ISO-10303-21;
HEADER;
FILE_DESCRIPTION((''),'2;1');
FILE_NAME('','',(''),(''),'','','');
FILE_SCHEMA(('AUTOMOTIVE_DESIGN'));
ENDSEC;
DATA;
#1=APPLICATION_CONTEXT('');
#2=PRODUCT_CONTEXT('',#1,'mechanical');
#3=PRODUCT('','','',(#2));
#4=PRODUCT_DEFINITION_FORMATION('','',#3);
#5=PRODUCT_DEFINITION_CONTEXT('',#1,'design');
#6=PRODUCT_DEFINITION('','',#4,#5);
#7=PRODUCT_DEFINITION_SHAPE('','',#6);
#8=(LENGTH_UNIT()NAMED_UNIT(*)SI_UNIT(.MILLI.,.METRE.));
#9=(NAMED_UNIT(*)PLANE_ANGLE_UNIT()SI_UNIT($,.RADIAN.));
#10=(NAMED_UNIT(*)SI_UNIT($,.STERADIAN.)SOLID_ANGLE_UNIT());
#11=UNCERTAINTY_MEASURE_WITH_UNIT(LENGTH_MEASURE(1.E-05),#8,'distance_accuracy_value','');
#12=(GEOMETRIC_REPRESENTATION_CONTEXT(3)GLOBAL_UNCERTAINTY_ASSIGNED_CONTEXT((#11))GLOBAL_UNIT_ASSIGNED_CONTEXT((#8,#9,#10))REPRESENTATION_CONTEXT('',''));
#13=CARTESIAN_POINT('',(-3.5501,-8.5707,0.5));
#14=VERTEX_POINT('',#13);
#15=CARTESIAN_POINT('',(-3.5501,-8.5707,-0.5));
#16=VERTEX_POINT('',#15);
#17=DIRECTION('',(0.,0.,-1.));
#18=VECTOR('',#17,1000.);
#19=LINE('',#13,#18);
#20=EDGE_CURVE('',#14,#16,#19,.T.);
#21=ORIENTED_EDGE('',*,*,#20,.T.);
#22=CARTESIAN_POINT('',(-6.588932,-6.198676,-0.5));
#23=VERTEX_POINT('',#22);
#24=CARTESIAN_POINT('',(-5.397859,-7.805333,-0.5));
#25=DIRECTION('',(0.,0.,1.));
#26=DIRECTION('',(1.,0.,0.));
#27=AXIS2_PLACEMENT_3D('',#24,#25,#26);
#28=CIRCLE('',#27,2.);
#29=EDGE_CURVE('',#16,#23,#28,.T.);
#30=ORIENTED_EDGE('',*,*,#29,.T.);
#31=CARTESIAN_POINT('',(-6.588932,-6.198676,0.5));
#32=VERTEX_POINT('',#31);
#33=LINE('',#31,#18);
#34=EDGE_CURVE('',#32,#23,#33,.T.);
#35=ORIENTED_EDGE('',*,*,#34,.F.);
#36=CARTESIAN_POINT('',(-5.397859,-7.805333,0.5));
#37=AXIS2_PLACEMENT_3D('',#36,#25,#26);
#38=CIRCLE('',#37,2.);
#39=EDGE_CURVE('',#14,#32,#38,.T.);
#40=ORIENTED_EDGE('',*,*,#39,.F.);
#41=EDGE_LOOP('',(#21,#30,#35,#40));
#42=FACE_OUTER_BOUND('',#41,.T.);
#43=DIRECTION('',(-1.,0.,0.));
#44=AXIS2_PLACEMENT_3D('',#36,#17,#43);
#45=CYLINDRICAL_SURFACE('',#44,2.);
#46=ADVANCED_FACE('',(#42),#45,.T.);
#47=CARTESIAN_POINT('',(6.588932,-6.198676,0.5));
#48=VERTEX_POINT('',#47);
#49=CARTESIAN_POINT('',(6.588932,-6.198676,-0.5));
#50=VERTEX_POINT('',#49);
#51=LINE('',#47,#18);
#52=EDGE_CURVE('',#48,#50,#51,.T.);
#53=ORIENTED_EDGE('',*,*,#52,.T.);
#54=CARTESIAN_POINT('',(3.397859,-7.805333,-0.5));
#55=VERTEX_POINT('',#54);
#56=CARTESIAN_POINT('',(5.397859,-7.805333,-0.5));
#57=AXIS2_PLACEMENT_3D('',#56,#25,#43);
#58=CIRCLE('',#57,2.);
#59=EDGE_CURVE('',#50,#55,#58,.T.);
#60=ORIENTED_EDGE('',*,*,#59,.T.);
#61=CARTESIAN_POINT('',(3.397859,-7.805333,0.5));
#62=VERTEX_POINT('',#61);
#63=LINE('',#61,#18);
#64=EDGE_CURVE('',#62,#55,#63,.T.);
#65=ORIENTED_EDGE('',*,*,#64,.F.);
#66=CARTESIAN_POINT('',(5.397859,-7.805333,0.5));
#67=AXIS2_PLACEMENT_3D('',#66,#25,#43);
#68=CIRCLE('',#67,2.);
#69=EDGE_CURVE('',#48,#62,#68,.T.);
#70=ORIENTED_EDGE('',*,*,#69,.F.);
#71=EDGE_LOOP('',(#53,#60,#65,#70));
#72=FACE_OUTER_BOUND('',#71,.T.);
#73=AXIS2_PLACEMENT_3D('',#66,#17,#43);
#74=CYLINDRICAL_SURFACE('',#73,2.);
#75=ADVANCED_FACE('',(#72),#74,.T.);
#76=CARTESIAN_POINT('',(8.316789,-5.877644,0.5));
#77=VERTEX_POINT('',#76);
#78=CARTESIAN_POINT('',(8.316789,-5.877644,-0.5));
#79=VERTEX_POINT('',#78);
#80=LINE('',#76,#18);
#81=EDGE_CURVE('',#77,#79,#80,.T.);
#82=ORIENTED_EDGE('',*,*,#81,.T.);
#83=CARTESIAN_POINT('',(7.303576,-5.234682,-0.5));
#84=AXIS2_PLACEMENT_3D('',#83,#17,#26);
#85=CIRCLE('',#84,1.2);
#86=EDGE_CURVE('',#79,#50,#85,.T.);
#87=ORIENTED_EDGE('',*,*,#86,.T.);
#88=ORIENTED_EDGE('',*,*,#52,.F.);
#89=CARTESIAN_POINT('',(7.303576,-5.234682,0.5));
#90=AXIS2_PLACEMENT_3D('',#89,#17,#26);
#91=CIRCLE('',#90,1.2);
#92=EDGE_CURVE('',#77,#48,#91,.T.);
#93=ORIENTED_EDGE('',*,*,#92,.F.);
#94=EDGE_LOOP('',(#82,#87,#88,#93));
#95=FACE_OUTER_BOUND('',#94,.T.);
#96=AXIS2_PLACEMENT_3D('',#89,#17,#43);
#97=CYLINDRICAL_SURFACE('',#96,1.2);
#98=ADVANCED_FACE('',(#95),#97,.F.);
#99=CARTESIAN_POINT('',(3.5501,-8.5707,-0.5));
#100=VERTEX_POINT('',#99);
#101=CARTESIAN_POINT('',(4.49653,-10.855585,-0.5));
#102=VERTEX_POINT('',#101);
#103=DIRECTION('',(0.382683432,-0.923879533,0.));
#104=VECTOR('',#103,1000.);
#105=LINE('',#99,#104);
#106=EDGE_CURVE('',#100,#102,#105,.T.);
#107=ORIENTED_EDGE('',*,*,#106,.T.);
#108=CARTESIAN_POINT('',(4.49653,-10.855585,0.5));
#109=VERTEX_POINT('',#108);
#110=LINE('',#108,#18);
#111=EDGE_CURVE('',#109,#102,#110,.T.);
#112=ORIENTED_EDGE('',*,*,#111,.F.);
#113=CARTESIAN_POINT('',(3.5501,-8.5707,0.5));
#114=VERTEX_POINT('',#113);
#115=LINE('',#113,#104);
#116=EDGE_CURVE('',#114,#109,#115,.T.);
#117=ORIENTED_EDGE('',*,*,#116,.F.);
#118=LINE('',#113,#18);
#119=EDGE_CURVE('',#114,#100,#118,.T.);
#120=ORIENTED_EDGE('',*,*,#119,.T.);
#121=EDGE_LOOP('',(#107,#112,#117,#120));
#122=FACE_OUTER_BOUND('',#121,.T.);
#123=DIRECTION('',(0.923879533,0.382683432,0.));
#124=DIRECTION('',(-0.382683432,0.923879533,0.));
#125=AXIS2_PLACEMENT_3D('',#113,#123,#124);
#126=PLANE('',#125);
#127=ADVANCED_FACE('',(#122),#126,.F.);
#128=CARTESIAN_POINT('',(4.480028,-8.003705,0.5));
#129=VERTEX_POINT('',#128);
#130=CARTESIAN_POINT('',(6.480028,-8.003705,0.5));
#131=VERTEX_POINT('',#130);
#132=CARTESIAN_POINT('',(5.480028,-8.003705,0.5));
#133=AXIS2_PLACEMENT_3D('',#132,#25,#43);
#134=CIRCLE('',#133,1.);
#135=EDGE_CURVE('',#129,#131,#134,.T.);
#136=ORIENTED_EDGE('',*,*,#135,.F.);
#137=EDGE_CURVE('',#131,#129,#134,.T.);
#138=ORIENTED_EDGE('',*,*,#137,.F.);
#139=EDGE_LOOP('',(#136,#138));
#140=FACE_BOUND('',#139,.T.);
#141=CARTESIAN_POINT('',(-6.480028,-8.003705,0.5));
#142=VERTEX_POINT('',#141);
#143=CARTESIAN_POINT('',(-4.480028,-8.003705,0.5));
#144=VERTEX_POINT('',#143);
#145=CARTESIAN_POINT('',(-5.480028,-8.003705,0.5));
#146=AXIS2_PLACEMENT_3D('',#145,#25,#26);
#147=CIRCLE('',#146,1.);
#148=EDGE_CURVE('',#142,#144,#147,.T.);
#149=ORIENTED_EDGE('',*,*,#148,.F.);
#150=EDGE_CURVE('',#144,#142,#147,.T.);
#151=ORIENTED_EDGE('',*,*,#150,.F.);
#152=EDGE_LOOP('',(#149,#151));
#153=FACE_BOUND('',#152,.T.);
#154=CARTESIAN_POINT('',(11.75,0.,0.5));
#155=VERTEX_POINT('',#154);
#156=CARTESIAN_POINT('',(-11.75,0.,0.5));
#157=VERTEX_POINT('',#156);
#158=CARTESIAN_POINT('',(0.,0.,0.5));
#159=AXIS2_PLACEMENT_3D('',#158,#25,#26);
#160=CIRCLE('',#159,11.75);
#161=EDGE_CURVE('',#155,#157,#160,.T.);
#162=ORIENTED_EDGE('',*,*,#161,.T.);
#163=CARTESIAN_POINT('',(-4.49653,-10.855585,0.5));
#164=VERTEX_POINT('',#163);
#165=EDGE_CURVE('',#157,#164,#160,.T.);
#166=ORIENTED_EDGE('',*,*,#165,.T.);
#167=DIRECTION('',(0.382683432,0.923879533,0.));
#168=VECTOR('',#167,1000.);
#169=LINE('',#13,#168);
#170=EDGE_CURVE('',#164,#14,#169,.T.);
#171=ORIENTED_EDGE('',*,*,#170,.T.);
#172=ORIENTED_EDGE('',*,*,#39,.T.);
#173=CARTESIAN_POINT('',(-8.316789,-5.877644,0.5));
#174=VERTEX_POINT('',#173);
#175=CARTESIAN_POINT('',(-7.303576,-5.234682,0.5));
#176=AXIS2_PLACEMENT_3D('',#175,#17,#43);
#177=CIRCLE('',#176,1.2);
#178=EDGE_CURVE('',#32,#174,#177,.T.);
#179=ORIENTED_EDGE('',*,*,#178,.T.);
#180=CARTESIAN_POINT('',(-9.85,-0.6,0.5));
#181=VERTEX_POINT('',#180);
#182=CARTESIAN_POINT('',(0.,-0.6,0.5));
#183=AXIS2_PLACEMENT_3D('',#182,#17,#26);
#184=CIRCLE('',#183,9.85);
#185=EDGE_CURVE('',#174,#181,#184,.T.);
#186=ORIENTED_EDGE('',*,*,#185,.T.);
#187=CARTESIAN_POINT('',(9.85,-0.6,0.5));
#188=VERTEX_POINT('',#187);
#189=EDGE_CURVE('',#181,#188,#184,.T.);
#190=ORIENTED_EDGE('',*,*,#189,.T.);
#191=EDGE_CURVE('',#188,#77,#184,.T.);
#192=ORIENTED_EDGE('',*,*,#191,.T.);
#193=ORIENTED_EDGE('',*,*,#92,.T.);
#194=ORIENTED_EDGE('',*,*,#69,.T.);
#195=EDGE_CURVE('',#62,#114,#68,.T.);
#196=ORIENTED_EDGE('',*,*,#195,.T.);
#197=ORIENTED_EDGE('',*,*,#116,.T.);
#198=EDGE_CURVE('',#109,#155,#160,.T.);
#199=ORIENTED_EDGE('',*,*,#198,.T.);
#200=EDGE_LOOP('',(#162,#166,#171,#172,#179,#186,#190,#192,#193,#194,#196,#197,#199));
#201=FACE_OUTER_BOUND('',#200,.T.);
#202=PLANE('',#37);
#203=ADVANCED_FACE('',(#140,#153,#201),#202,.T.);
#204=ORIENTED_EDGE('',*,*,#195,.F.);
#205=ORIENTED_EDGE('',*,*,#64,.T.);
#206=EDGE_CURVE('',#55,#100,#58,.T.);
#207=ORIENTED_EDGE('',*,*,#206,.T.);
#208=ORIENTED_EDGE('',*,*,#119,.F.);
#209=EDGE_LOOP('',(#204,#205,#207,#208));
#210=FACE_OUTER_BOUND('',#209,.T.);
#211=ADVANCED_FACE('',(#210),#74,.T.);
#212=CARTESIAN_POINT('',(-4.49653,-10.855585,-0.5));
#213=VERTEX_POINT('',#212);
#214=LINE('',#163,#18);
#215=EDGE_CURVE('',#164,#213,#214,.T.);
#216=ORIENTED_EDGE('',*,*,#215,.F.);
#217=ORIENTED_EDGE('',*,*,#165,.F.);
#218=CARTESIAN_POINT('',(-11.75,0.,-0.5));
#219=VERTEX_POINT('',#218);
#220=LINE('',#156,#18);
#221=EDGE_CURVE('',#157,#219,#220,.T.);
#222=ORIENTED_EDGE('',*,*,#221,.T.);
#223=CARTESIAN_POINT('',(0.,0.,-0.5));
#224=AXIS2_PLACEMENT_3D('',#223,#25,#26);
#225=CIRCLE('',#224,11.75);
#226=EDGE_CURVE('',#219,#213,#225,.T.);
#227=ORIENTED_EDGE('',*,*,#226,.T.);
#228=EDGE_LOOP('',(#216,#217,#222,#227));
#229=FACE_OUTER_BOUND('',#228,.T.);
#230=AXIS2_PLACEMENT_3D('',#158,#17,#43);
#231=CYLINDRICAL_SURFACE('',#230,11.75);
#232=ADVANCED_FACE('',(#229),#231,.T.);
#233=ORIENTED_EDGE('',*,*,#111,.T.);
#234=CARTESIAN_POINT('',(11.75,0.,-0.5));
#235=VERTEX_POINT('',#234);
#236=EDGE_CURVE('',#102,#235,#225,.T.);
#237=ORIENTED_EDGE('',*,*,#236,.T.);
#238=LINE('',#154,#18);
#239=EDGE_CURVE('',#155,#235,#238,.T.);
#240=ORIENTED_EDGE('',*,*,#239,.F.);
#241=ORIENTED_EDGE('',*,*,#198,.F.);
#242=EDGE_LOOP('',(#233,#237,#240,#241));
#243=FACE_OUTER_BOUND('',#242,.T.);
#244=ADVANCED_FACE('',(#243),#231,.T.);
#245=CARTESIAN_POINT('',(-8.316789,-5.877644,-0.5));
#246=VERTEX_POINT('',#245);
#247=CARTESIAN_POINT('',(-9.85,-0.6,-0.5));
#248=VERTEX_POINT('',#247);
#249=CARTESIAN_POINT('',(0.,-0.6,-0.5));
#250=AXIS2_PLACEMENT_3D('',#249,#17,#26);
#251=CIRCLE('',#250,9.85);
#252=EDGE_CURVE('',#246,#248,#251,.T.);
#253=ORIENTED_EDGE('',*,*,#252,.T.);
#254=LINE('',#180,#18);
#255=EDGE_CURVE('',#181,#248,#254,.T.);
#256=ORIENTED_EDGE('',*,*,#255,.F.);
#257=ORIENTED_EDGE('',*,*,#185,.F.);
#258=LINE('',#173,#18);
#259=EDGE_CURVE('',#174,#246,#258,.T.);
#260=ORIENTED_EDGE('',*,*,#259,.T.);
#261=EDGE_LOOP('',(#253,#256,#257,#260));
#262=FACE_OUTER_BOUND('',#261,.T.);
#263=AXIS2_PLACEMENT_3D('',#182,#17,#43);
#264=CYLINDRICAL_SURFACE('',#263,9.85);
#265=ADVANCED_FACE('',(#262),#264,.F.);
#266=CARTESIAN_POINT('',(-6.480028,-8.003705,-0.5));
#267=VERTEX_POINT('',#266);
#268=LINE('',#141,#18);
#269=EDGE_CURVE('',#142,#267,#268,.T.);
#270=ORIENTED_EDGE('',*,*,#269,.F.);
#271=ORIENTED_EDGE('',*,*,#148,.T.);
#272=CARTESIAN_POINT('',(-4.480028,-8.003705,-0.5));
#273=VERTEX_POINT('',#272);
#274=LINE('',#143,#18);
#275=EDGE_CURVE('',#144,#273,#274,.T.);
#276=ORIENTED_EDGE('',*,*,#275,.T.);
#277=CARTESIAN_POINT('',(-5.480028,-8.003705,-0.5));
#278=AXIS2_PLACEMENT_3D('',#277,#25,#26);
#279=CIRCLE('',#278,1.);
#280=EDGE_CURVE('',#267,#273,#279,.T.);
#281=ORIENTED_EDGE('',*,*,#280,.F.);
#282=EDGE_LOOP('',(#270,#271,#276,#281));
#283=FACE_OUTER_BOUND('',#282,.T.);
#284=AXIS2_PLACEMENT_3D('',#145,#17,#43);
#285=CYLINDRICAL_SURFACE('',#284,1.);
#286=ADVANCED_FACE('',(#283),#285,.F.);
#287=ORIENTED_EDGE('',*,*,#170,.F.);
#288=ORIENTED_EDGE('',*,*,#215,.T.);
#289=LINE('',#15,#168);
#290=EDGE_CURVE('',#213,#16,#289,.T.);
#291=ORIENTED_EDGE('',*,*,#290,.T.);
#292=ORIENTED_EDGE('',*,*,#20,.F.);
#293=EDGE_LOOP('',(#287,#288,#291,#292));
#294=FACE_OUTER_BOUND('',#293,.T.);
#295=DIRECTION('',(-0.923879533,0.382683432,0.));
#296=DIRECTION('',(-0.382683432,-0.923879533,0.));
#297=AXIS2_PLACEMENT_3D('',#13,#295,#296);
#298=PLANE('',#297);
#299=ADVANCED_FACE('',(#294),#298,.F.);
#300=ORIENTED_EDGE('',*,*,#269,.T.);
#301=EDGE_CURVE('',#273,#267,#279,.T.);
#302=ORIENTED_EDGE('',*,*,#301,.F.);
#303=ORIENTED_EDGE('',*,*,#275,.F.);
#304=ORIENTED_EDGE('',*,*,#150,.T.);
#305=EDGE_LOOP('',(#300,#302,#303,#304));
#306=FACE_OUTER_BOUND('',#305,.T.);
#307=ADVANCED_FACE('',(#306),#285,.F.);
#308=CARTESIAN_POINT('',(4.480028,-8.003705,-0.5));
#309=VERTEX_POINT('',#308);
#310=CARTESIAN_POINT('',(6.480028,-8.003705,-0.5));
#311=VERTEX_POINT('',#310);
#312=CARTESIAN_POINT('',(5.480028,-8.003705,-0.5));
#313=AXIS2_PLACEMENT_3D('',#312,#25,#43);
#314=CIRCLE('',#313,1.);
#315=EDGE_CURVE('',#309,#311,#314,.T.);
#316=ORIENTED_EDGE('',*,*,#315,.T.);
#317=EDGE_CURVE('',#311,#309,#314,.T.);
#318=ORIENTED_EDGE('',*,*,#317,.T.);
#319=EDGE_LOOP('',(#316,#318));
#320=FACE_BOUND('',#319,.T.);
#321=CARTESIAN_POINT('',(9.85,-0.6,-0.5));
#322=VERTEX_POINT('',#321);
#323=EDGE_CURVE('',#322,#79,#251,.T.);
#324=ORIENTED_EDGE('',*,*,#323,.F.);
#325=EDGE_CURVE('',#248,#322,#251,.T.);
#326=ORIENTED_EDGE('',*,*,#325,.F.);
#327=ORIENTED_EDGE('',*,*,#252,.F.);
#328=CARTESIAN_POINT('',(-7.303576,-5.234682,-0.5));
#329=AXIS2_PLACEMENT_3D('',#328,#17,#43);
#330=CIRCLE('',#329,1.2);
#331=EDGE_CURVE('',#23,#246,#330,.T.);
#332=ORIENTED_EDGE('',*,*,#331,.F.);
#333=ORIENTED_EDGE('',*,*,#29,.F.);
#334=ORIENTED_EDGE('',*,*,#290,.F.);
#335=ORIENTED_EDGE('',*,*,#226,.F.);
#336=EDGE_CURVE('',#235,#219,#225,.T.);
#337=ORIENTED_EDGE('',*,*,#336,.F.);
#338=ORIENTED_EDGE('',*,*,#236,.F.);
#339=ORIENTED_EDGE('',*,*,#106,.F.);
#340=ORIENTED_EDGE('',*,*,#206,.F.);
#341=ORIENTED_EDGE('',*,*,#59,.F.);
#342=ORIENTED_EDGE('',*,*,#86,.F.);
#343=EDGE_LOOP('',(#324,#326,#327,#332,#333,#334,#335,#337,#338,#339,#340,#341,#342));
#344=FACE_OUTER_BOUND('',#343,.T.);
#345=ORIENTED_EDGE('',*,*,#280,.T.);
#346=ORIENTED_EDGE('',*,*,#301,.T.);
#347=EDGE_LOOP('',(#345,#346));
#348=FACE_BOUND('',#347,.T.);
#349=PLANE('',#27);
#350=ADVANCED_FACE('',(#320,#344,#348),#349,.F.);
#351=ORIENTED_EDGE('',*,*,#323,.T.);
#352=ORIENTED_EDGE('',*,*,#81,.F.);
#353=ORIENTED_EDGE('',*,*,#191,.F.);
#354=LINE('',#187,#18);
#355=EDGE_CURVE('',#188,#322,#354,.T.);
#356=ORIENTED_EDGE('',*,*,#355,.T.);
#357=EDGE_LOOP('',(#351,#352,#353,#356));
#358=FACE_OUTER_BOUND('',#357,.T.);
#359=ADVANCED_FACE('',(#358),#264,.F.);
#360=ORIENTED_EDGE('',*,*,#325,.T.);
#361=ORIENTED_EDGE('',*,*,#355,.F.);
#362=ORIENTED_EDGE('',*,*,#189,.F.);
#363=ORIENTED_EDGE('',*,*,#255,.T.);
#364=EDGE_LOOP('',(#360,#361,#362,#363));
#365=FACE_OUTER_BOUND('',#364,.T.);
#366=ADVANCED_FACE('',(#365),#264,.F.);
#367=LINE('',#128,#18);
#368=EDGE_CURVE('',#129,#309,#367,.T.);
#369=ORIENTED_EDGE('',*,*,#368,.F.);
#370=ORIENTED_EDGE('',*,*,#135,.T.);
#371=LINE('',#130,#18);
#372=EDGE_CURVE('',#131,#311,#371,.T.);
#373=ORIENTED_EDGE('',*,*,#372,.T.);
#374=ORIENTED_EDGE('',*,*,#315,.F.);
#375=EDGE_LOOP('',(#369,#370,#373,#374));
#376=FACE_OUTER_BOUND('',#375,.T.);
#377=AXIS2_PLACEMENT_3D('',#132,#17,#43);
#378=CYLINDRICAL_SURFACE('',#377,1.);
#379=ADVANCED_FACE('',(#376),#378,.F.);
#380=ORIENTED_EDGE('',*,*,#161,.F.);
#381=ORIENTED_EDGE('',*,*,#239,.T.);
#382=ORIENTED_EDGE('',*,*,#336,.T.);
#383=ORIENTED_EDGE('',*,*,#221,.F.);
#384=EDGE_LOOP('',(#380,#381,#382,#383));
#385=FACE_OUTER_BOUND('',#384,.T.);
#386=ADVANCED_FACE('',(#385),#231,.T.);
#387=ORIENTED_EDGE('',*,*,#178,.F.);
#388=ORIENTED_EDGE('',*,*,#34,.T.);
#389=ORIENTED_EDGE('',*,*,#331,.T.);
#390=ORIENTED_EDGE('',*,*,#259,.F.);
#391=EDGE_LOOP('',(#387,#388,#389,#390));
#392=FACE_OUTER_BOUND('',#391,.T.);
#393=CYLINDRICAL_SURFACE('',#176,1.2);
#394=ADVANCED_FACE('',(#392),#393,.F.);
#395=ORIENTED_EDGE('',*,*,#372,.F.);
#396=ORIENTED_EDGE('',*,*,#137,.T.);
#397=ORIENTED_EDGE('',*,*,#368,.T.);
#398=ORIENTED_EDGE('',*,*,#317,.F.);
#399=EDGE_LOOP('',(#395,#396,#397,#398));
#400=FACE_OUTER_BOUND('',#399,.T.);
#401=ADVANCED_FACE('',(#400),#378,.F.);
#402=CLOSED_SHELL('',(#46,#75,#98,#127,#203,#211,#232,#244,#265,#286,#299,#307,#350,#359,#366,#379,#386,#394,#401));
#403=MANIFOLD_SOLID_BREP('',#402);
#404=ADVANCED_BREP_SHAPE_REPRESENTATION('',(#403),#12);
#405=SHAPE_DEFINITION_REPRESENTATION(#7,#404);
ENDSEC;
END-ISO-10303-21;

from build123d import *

# Parameters (mm, degrees)
BASE_EXTRUDE_DEPTH      = 0.5
BASE_EXTRUDE_DEPTH_BACK = 0.5
SKETCH1_R               = 1


with BuildPart() as part:
    # Sketch1 → Base-Extrude (new, two sides: drawn at the far end of the back side and taken through both)
    with BuildSketch(Plane.XY.offset(-BASE_EXTRUDE_DEPTH_BACK)):
        with BuildLine():
            Line((-3.550099977, -8.570699513), (-4.49653033, -10.855584507))
            ThreePointArc((-4.49653033, -10.855584507), (0, 11.75), (4.49653033, -10.855584507))
            Line((4.49653033, -10.855584507), (3.550099977, -8.570699513))
            ThreePointArc((3.550099977, -8.570699513), (4.167236093, -6.228764491), (6.588932053, -6.198676157))
            ThreePointArc((6.588932053, -6.198676157), (7.52278189, -6.414491024), (8.316788695, -5.877643962))
            ThreePointArc((8.316788695, -5.877643962), (0, 9.25), (-8.316788695, -5.877643962))
            ThreePointArc((-8.316788695, -5.877643962), (-7.52278189, -6.414491024), (-6.588932053, -6.198676157))
            ThreePointArc((-6.588932053, -6.198676157), (-4.167236093, -6.228764491), (-3.550099977, -8.570699513))
        make_face()
        with Locations((-5.480027646, -8.003705205)):
            Circle(SKETCH1_R, mode=Mode.SUBTRACT)
        with Locations(Location((5.480027646, -8.003705205, 0), (0, 0, 180))):
            Circle(SKETCH1_R, mode=Mode.SUBTRACT)
    extrude(amount=BASE_EXTRUDE_DEPTH + BASE_EXTRUDE_DEPTH_BACK)


solid = part.part
